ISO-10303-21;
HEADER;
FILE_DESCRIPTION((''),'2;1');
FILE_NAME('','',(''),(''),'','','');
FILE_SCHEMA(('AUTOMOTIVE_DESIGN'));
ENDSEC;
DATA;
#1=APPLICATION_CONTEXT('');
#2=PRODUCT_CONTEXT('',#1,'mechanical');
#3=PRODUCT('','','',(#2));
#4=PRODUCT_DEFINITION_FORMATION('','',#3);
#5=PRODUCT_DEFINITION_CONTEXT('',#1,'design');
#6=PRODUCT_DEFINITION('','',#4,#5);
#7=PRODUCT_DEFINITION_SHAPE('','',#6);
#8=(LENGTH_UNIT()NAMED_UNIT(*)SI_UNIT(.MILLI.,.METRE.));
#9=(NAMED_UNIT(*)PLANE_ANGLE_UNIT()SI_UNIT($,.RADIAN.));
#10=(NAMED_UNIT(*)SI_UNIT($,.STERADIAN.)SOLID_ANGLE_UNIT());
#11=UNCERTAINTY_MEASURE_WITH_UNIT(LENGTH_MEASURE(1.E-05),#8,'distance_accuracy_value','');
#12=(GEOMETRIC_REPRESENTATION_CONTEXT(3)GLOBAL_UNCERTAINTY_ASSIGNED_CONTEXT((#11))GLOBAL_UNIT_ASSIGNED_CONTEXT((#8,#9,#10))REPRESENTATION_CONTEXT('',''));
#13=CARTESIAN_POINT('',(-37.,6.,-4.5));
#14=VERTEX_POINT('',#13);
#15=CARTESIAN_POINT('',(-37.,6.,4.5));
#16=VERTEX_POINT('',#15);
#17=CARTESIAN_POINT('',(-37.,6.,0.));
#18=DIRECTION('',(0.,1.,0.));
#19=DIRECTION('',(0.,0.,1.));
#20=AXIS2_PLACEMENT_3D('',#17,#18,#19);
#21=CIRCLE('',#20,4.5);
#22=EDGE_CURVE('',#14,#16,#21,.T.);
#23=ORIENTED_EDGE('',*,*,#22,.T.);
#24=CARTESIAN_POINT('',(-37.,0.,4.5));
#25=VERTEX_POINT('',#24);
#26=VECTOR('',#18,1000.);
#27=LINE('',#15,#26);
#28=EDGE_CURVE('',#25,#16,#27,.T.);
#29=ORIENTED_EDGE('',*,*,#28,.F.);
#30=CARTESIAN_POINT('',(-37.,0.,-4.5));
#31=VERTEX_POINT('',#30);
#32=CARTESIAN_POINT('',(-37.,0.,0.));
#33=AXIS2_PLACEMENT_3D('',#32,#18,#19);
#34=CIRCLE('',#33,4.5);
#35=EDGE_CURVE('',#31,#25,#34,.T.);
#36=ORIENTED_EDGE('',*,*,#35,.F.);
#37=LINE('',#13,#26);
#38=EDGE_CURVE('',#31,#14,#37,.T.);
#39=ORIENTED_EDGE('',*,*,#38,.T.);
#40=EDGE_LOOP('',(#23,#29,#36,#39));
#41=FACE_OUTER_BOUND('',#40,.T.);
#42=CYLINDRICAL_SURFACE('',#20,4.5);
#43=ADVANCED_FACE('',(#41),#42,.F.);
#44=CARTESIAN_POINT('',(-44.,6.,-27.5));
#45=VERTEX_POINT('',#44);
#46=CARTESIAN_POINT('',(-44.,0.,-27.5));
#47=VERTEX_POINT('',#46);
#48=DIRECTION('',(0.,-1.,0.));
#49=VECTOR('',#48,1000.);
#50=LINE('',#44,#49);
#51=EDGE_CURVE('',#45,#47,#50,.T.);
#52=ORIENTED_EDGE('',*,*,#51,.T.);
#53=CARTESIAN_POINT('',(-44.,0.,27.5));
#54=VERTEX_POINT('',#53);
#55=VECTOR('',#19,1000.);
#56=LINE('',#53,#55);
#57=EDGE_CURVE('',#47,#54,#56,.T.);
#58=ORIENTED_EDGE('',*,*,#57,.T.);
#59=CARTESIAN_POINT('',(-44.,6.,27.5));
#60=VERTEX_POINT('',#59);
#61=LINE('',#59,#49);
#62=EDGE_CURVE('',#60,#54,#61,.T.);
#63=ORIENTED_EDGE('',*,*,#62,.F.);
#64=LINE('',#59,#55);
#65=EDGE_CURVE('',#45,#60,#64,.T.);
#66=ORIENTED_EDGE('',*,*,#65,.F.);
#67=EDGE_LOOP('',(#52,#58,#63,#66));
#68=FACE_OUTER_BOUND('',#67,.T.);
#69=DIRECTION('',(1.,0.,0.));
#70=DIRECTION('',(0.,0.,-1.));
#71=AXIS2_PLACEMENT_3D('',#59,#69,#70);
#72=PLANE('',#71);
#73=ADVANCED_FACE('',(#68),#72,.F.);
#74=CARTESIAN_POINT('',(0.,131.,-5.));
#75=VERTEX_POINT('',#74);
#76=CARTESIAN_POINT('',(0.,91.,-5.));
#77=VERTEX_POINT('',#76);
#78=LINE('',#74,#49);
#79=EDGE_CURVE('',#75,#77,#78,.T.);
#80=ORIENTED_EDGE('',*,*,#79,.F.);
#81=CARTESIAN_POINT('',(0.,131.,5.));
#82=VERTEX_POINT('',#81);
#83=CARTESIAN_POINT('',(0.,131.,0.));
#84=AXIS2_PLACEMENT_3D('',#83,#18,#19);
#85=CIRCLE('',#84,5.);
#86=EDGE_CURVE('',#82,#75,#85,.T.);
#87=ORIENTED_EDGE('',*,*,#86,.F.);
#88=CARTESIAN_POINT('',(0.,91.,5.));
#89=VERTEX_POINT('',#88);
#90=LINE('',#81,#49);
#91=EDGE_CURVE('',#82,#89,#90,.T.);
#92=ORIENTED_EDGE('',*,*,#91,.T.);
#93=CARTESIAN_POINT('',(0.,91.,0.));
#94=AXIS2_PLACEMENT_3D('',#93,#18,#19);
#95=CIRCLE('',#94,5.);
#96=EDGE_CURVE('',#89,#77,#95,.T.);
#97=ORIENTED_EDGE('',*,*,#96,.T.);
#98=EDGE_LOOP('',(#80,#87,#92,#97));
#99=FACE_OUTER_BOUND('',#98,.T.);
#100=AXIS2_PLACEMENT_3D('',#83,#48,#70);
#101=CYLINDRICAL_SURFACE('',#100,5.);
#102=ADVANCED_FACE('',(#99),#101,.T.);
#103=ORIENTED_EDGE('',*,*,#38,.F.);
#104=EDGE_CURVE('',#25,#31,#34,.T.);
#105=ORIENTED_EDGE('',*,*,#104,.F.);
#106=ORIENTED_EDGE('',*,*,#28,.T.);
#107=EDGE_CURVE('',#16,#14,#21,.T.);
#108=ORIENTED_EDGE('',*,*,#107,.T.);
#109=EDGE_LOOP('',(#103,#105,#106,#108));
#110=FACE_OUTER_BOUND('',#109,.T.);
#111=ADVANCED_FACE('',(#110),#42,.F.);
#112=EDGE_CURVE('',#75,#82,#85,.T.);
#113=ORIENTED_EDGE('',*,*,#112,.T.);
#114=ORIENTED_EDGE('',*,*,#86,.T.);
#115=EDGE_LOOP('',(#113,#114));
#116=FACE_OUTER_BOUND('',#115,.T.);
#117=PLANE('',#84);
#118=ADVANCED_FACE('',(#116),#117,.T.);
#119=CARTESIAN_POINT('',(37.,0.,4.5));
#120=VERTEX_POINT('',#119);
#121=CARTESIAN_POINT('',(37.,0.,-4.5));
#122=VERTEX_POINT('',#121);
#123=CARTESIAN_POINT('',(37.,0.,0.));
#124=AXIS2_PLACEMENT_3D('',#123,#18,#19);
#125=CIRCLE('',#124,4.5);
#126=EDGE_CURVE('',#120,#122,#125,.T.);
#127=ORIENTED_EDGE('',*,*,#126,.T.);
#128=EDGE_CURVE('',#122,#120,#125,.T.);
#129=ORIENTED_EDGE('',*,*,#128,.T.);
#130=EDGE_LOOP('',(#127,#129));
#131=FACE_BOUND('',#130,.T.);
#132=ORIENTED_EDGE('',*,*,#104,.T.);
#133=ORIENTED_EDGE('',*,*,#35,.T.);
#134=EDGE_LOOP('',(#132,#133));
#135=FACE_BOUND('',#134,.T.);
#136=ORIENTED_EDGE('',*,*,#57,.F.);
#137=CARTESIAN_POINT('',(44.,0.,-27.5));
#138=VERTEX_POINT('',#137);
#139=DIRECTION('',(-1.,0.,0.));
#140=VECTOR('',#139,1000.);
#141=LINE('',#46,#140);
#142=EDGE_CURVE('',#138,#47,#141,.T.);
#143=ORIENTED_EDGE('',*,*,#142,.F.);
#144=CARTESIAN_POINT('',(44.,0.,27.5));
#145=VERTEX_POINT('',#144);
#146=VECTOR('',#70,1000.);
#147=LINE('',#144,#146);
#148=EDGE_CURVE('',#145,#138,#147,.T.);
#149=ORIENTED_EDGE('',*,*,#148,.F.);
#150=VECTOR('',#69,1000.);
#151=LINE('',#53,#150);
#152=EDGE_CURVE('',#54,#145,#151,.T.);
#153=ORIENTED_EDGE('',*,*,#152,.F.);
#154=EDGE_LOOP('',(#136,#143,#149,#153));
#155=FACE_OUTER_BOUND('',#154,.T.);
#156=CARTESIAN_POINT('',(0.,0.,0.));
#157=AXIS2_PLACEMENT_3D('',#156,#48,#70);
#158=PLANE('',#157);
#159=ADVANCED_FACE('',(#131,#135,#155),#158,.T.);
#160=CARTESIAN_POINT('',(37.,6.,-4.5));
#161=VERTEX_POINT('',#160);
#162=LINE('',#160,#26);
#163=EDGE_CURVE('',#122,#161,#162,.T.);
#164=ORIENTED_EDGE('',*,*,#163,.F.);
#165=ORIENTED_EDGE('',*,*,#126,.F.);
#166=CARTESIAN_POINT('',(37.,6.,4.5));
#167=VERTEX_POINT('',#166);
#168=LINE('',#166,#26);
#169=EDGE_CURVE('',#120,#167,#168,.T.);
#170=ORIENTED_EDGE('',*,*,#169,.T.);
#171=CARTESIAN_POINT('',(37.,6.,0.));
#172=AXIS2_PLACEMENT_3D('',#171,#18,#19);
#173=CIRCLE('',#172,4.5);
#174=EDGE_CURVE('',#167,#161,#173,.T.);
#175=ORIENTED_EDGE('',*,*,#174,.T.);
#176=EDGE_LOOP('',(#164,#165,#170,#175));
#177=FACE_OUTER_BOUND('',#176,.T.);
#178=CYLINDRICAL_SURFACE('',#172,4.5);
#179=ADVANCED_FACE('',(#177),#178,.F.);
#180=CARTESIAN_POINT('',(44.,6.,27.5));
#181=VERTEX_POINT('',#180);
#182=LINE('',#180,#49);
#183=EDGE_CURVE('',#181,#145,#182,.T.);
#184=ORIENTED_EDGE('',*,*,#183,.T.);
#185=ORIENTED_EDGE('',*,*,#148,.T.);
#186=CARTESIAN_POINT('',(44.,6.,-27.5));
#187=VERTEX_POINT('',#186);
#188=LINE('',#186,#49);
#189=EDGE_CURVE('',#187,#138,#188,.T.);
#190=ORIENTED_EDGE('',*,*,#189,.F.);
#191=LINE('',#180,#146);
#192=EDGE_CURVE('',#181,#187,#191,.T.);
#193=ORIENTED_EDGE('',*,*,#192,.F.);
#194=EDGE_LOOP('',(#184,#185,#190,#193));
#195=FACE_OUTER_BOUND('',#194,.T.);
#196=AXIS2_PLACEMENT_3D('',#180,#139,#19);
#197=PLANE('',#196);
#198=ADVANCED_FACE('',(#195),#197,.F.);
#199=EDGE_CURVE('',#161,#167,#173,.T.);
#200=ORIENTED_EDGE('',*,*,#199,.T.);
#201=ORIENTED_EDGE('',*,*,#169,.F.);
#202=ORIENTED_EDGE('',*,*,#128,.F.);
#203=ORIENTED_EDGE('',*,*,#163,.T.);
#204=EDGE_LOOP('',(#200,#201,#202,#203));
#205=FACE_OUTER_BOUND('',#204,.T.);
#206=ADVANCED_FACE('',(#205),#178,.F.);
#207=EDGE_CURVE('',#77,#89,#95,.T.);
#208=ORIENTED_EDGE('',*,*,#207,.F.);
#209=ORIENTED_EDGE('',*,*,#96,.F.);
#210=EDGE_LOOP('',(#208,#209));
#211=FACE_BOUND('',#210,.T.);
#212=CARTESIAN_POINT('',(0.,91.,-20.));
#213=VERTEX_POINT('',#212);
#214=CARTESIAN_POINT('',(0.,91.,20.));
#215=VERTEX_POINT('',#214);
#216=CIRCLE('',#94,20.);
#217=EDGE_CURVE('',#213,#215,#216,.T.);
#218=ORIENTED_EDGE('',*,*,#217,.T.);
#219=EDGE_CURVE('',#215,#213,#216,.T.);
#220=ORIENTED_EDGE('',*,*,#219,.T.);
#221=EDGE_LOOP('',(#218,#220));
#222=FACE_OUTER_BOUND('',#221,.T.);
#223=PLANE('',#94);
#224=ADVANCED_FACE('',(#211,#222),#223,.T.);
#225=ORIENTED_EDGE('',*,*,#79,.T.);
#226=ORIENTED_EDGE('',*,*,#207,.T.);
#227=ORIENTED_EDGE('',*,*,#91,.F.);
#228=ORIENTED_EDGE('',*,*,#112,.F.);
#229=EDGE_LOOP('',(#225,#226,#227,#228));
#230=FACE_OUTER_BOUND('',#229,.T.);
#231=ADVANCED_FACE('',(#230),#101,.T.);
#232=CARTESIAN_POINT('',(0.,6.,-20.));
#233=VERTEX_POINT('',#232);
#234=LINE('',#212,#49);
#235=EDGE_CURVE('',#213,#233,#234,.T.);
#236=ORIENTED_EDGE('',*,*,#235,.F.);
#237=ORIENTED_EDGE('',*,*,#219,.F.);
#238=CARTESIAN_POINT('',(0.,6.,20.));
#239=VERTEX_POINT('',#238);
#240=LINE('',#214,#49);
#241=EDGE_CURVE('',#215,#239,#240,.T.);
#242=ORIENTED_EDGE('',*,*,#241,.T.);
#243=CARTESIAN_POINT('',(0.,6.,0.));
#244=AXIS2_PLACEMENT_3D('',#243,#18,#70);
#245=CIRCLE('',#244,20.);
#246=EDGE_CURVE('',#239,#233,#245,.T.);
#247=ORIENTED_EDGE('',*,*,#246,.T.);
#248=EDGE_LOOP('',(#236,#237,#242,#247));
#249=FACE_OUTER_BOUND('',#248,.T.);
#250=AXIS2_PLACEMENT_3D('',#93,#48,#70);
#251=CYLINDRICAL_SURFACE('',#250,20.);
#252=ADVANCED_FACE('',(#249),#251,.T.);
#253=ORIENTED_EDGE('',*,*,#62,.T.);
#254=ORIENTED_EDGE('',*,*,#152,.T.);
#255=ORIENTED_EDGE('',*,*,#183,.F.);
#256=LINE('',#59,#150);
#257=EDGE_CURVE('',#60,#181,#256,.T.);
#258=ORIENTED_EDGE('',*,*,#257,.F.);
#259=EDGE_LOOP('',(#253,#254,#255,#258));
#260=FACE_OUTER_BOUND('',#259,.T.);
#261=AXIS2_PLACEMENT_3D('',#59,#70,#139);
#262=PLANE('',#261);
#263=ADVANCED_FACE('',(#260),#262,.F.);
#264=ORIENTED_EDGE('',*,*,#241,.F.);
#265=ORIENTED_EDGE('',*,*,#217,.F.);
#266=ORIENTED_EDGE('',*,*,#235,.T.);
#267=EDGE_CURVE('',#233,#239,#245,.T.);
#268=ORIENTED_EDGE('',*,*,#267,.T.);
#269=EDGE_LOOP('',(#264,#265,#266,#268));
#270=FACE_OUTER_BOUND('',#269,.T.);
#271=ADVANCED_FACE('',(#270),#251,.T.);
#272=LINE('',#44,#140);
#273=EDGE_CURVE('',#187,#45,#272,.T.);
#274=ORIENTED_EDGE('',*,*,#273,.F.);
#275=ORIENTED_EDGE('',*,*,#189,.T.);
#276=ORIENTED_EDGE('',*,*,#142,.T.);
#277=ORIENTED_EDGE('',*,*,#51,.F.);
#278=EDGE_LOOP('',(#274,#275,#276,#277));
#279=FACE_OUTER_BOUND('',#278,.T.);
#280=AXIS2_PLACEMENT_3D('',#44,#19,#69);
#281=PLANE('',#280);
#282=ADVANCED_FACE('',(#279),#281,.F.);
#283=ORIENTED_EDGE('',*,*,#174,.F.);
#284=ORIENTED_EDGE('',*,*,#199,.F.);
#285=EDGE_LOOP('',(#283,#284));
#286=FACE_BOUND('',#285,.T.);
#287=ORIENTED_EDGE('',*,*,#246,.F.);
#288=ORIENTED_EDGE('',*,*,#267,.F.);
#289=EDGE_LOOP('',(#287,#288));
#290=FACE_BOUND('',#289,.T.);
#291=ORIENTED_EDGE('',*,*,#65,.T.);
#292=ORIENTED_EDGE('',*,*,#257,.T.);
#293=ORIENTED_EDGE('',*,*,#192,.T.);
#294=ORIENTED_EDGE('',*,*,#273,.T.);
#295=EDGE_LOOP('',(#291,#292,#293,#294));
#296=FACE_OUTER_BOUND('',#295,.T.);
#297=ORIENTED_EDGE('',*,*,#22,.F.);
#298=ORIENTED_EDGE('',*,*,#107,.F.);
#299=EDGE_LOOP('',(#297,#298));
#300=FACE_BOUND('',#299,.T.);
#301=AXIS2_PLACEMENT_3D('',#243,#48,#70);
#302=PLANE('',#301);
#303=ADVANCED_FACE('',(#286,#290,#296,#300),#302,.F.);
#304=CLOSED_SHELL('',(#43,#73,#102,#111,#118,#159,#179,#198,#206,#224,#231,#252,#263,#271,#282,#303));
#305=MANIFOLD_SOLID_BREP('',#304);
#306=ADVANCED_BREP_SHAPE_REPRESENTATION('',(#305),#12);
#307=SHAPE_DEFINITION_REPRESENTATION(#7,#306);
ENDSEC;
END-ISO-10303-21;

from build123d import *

# Parameters (mm, degrees)
SKETCH_1_W         = 88
SKETCH_1_H         = 55
EXTRUDE_1_DEPTH    = 6
HOLE_WIZARD_M8_1_D = 9
SKETCH_4_R         = 20
EXTRUDE_2_DEPTH    = 85
SKETCH_5_R         = 5
EXTRUDE_3_DEPTH    = 40


with BuildPart() as part:
    # 草图1 → 凸台-拉伸1 (new body)
    with BuildSketch(Plane(origin=(0, 0, 0), x_dir=(1, 0, 0), z_dir=(0, 1, 0))):
        Rectangle(SKETCH_1_W, SKETCH_1_H)
    extrude(amount=EXTRUDE_1_DEPTH)

    # M8 间隙孔1 (through all)
    with Locations(Plane(origin=(0, 6, 0), x_dir=(1, 0, 0), z_dir=(0, 1, 0))):
        with Locations((-37, 0), (37, 0)):
            Hole(HOLE_WIZARD_M8_1_D / 2)

    # 草图4 → 凸台-拉伸2 (add)
    with BuildSketch(Plane(origin=(0, 6, 0), x_dir=(1, 0, 0), z_dir=(0, 1, 0))):
        with Locations(Location((0, 0, 0), (0, 0, 90))):
            Circle(SKETCH_4_R)
    extrude(amount=EXTRUDE_2_DEPTH)

    # 草图5 → 凸台-拉伸3 (add)
    with BuildSketch(Plane(origin=(0, 91, 0), x_dir=(1, 0, 0), z_dir=(0, 1, 0))):
        with Locations(Location((0, 0, 0), (0, 0, 270))):
            Circle(SKETCH_5_R)
    extrude(amount=EXTRUDE_3_DEPTH)


solid = part.part
